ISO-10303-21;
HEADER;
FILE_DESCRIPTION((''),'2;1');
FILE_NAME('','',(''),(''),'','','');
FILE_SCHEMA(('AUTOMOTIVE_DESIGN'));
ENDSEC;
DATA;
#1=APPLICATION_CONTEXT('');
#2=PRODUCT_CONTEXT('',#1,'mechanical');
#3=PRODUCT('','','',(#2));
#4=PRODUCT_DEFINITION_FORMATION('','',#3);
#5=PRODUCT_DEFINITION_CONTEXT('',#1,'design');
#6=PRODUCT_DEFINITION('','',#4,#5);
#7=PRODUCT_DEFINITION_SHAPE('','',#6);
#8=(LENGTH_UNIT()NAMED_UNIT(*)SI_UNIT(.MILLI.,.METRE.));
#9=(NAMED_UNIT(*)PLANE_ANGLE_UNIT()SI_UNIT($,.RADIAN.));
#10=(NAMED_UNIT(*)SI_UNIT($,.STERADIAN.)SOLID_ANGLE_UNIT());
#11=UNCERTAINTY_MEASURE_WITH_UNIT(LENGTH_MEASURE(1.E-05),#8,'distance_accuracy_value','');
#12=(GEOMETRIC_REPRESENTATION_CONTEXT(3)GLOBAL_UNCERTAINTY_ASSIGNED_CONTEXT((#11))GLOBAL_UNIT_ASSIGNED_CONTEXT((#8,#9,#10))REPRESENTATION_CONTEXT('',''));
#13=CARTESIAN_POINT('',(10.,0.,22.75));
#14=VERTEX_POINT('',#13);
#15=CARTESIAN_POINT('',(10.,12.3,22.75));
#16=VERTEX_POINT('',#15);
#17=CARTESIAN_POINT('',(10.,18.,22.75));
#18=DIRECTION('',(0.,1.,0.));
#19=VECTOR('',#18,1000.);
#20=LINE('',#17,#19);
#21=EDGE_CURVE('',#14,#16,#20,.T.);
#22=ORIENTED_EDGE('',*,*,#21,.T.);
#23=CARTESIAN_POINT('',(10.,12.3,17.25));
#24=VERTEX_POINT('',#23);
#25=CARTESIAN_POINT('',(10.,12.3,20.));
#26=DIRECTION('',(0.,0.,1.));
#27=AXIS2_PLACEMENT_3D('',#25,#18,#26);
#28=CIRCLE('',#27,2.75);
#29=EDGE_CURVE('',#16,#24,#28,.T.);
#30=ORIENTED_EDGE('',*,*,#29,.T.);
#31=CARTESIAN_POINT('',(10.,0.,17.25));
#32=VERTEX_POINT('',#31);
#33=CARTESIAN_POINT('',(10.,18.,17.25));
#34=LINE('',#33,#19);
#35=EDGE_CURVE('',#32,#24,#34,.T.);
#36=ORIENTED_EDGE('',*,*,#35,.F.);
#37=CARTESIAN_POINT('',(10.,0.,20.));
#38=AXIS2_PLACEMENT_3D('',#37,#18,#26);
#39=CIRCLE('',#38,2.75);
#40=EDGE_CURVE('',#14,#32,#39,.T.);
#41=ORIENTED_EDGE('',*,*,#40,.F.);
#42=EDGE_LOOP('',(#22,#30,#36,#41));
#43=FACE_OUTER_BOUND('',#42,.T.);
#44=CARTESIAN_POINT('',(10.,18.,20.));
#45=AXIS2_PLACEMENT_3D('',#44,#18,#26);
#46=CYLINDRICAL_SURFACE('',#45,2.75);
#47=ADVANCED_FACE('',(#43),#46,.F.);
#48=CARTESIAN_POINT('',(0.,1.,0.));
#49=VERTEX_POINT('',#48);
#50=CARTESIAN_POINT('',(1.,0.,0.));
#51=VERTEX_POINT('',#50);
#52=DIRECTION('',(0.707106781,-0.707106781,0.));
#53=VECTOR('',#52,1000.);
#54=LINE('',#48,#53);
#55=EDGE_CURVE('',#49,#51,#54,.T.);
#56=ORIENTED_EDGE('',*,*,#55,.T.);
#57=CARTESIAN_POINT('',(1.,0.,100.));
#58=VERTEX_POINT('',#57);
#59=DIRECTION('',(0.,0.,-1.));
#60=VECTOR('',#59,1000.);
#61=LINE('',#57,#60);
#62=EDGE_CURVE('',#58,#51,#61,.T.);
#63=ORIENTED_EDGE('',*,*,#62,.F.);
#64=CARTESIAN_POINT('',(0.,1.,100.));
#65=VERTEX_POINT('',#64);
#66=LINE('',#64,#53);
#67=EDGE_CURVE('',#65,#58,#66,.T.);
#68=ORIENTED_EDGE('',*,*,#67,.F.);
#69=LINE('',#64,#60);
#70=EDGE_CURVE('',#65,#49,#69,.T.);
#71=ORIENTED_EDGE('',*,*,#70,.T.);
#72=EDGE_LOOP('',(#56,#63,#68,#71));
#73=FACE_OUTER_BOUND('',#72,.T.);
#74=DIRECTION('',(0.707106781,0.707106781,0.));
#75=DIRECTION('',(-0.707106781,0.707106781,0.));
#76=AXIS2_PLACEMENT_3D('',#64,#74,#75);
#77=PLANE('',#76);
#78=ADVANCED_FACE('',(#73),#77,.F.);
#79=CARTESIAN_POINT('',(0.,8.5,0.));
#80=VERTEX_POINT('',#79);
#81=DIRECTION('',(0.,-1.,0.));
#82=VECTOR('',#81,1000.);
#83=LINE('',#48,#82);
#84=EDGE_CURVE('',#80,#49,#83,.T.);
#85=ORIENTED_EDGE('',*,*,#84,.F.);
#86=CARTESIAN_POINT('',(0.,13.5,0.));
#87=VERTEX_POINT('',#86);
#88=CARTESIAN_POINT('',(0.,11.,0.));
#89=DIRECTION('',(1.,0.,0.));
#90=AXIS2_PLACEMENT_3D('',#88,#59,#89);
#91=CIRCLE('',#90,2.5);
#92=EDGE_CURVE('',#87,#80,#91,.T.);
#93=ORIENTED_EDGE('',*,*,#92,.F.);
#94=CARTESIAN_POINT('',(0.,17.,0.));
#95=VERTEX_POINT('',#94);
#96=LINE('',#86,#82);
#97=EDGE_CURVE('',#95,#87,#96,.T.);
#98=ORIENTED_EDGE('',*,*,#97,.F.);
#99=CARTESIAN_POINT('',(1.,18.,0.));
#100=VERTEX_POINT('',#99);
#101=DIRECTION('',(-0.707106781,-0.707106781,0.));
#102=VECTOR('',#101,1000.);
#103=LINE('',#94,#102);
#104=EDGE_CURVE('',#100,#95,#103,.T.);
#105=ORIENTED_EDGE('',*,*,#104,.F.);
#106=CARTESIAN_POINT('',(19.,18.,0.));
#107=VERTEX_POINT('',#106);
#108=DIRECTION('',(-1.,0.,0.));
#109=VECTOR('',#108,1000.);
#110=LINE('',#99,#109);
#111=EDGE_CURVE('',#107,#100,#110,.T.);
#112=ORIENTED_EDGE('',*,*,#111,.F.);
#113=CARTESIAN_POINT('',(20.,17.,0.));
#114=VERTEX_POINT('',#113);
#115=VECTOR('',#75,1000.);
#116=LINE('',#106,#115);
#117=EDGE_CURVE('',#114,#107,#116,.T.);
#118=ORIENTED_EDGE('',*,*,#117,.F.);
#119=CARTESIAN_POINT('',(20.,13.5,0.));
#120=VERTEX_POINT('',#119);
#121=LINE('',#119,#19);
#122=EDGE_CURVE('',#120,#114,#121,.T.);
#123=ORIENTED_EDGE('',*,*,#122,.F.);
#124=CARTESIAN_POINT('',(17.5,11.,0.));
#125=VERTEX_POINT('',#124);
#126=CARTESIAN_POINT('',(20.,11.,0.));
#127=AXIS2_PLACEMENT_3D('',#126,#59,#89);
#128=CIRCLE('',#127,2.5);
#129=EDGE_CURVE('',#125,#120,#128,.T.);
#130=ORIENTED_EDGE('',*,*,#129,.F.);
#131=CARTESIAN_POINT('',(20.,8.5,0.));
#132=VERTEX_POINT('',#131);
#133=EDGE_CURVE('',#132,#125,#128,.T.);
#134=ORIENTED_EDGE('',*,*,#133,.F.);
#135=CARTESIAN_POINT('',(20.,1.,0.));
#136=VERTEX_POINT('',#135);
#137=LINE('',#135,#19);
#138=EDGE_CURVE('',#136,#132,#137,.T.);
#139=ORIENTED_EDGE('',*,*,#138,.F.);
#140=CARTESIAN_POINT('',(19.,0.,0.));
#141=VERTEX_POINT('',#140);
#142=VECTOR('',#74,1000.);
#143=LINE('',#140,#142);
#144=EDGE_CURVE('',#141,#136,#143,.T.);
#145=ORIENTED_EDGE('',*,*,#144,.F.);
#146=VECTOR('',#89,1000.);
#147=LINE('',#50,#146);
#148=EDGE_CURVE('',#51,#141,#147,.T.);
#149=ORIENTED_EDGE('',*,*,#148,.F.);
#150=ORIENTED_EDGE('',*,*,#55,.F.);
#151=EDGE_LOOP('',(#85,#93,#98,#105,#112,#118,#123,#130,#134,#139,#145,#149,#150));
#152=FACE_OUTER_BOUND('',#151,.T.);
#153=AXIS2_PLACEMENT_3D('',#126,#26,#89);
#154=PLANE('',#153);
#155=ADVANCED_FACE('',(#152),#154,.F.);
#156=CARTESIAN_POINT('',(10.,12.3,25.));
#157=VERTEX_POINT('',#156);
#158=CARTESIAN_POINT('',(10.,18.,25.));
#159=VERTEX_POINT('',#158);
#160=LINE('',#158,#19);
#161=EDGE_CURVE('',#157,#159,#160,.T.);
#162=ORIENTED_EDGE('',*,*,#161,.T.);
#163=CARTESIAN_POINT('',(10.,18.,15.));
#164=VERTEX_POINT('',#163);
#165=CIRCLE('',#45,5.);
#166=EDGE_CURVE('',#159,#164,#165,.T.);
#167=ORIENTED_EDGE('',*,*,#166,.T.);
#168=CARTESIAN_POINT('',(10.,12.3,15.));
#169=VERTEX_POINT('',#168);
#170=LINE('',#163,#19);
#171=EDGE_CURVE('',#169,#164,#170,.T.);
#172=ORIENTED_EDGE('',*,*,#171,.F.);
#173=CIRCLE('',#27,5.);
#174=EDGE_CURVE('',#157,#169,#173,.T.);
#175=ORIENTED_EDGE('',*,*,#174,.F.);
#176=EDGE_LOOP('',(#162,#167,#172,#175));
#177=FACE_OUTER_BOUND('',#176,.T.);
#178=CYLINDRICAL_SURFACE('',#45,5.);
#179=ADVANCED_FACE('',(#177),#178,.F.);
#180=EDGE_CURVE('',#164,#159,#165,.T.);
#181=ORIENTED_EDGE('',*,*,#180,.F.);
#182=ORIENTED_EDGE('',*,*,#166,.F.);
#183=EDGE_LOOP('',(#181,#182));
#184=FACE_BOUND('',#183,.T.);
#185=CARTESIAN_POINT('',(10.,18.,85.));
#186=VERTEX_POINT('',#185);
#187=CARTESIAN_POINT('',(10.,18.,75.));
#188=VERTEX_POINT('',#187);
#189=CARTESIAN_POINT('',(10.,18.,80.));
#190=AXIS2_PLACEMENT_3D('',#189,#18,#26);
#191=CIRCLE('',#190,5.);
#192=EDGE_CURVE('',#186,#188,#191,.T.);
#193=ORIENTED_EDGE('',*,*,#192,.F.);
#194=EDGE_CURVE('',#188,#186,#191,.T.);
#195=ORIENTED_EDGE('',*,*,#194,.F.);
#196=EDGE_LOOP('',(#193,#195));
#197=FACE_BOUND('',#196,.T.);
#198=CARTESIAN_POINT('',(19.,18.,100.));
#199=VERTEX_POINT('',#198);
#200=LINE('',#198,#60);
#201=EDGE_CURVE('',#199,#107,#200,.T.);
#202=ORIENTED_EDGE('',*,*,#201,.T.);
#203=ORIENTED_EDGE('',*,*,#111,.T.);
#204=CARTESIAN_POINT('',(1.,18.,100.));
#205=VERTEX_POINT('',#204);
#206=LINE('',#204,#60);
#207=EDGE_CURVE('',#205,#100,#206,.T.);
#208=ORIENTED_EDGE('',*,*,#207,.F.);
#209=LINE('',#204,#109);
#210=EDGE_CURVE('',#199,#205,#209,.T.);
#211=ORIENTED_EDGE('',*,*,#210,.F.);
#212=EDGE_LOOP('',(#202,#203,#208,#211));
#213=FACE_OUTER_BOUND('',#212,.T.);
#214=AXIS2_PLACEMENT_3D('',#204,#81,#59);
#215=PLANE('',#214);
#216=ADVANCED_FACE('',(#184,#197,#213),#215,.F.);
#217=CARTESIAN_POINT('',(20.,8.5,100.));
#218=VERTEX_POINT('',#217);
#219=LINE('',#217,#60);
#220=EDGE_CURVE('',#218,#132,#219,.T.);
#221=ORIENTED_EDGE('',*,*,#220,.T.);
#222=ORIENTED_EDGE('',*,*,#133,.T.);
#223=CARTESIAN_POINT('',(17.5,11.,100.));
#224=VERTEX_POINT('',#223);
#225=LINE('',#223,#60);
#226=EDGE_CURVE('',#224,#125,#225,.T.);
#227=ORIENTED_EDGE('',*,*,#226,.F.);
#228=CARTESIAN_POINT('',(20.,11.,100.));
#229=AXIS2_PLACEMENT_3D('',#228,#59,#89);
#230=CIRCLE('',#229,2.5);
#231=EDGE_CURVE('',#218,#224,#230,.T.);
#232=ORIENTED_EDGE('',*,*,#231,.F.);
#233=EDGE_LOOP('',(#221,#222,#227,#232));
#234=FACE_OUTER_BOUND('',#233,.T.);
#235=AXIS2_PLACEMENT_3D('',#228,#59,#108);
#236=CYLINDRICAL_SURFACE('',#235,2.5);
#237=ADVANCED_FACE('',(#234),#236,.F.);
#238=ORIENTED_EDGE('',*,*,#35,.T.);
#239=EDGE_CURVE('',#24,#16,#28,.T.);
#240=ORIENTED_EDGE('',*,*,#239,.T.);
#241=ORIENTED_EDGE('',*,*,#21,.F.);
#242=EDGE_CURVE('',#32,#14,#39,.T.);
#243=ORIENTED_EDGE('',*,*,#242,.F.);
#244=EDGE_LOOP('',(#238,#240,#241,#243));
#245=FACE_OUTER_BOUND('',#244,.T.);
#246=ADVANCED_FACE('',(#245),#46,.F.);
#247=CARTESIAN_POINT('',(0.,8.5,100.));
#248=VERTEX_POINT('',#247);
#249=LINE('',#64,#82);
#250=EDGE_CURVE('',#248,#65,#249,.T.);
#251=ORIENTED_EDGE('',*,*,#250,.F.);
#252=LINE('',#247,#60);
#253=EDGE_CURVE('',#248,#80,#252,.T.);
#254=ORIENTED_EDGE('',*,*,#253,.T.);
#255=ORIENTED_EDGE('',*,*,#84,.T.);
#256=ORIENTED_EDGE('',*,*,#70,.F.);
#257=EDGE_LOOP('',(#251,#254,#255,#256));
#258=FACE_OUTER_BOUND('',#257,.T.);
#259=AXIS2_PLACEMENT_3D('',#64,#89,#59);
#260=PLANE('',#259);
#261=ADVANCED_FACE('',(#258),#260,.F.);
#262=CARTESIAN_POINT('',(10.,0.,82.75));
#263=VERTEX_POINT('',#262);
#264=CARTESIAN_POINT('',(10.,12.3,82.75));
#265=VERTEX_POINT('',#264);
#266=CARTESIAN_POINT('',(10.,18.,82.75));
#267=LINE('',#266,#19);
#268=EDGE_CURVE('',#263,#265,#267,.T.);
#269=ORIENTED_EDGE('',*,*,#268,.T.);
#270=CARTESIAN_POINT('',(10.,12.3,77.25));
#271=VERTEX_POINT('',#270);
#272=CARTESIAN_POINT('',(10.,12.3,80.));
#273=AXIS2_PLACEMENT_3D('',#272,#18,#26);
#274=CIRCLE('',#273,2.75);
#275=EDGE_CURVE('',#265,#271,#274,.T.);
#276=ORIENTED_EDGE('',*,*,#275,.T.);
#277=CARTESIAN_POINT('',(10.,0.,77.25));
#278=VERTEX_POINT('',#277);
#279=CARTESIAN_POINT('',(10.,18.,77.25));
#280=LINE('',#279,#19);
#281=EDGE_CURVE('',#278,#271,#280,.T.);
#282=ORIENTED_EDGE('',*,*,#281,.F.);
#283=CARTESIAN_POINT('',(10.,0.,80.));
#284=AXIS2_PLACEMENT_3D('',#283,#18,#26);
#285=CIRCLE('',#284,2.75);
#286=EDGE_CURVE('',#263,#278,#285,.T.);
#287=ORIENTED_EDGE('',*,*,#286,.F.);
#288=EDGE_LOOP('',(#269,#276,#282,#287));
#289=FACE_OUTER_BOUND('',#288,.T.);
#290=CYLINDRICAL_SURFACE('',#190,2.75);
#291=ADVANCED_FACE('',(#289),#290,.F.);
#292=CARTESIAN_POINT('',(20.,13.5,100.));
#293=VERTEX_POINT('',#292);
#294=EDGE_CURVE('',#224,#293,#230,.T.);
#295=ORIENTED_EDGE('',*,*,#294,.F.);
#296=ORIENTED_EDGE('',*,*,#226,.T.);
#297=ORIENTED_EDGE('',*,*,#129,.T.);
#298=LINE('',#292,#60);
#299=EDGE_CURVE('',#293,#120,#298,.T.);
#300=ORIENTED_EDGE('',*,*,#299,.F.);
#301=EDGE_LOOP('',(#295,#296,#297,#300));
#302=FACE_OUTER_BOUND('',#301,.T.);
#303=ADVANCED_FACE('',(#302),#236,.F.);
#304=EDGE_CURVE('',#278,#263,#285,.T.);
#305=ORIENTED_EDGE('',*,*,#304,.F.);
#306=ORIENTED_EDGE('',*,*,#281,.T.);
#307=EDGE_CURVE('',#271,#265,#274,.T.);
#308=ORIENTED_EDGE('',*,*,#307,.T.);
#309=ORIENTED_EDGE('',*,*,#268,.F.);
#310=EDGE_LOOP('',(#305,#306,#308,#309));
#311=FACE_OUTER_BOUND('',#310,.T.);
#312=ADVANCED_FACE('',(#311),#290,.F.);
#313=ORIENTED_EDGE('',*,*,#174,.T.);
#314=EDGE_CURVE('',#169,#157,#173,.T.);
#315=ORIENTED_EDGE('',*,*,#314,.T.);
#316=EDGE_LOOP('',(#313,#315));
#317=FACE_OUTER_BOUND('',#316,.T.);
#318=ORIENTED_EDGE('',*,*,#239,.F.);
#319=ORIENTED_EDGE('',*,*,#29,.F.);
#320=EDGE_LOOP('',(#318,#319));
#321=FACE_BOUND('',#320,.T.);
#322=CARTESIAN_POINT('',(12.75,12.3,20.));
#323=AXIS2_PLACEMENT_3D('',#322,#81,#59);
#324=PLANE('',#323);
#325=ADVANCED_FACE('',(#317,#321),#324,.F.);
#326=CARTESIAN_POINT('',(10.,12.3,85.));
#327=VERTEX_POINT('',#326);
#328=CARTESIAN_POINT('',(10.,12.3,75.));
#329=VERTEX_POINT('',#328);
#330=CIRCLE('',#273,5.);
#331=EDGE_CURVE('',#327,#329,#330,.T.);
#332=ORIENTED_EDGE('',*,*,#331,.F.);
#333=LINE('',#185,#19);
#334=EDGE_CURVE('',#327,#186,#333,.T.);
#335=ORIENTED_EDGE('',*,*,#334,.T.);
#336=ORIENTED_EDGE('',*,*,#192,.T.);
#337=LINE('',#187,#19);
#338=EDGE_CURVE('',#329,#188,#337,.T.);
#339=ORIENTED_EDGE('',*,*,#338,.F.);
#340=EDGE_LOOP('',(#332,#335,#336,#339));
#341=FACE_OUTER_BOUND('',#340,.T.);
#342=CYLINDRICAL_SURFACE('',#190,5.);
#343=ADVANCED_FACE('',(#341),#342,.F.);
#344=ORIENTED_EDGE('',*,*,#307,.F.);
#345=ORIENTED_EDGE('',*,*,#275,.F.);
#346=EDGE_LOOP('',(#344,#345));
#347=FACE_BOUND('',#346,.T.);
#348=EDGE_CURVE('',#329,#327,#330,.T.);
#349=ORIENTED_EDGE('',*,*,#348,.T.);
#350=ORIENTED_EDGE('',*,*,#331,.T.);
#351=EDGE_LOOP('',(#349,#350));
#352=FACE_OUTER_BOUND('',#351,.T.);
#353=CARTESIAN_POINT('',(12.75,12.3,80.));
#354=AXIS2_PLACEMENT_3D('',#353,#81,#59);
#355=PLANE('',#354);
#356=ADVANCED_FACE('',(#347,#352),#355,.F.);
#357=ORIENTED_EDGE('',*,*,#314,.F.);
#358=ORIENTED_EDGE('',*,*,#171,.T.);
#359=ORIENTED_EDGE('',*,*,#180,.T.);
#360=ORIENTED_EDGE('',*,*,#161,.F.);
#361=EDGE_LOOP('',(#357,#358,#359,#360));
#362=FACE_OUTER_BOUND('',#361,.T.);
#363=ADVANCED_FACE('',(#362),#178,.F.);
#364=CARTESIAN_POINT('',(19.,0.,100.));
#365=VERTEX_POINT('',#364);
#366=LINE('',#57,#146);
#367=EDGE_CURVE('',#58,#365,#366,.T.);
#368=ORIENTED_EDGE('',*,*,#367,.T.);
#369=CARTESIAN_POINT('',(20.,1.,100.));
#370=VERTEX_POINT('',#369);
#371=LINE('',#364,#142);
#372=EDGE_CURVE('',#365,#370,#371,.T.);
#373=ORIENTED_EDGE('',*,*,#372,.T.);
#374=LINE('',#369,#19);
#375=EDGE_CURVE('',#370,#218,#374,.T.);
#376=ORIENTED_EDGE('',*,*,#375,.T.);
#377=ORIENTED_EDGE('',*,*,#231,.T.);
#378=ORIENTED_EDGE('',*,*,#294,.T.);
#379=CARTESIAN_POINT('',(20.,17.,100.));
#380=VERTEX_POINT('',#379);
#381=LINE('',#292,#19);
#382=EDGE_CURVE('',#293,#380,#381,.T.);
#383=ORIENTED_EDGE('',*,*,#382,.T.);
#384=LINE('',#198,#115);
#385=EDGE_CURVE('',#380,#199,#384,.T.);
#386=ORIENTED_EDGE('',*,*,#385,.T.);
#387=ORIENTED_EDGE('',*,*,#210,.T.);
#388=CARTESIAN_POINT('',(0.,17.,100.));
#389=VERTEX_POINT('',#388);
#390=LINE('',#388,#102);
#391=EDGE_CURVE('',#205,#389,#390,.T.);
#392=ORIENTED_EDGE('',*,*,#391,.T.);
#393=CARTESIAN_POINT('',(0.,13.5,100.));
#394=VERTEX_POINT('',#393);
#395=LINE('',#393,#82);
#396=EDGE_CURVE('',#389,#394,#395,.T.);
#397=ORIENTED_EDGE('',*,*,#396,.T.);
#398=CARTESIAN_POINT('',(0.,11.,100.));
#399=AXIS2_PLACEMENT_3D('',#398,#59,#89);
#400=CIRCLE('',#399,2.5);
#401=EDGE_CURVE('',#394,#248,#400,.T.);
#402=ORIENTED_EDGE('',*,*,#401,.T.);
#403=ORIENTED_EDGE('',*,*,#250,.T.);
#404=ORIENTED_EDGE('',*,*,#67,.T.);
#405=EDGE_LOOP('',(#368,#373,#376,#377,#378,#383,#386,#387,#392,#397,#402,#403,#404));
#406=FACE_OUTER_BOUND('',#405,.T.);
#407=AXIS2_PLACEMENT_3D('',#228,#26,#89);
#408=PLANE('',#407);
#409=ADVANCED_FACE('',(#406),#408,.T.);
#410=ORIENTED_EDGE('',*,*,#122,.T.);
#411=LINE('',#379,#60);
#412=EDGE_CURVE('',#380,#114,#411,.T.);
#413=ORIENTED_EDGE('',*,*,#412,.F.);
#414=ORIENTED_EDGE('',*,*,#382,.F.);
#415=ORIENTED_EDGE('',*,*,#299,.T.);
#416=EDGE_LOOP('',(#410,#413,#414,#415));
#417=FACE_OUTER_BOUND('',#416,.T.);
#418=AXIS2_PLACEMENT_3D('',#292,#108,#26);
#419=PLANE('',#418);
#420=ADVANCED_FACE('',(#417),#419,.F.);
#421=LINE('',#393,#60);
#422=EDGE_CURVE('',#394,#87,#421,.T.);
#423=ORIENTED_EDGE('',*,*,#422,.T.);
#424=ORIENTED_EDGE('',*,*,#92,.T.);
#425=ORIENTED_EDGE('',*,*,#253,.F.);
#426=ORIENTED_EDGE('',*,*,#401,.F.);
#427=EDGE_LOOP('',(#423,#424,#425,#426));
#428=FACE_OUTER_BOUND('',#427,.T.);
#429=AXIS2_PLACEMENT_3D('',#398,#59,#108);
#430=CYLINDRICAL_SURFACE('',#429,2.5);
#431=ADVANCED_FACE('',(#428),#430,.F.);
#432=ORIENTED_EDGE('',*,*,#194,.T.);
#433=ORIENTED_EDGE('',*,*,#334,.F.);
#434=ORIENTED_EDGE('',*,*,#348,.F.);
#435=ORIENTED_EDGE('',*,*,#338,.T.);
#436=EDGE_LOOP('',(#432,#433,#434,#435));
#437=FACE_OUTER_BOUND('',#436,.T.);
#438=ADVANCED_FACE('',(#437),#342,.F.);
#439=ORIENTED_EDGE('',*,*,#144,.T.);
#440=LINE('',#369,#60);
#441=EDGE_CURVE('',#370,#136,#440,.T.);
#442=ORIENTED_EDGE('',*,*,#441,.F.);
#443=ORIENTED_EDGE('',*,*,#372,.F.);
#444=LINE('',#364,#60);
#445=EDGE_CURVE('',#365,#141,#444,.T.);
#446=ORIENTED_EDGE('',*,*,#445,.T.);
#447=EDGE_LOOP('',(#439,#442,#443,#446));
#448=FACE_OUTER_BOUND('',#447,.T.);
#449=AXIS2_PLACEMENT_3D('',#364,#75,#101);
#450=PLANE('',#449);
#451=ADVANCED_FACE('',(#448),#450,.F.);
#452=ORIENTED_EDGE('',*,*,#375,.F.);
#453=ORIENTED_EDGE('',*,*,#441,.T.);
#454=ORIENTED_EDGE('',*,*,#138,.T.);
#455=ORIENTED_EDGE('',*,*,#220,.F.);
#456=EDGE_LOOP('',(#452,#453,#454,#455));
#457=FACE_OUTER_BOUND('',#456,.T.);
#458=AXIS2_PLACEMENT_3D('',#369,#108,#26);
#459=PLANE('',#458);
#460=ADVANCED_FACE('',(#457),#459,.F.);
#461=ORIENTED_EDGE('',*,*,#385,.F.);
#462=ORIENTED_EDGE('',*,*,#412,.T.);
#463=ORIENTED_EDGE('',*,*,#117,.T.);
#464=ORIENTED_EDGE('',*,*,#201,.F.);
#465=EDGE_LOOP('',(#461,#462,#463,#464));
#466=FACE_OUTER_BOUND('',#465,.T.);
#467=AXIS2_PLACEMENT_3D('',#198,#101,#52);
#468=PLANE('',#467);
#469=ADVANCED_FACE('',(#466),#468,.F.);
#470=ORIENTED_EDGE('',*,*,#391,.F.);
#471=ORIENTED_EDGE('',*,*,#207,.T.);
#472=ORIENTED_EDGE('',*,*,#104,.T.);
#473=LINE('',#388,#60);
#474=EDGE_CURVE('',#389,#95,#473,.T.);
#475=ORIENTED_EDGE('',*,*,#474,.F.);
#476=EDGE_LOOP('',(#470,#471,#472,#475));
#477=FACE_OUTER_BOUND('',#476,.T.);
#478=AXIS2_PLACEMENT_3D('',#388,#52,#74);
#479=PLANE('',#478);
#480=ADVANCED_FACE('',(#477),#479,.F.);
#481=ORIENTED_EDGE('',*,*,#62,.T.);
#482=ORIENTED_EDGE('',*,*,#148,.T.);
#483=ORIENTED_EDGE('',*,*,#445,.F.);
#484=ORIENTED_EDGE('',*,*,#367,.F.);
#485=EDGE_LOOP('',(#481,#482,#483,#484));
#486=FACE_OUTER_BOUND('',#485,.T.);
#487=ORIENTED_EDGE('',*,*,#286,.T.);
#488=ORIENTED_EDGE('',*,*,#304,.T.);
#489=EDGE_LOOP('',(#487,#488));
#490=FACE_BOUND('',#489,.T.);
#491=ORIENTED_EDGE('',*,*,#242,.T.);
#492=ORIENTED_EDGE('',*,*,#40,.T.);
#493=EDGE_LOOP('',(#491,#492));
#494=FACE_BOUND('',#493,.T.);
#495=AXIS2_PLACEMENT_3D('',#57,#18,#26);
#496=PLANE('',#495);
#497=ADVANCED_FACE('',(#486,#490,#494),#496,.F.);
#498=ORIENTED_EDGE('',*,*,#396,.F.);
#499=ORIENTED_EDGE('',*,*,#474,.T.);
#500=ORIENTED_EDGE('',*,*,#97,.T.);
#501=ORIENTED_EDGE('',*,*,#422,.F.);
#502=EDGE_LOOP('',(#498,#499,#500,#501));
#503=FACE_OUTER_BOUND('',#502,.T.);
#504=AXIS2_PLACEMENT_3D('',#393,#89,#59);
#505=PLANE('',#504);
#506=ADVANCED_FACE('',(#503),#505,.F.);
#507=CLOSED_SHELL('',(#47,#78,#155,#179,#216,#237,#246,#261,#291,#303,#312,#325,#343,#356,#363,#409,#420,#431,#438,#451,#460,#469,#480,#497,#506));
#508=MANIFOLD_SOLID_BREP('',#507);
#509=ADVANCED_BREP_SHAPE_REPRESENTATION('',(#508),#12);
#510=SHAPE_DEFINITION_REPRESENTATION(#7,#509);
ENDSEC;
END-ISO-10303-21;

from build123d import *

# Parameters (mm, degrees)
EXTRUDE1_DEPTH                                       = 100
HOLE_SIZE_PER_SOCKET_HEAD_CAP_SCREW_TYPE_D           = 5.5
HOLE_SIZE_PER_SOCKET_HEAD_CAP_SCREW_TYPE_CBORE_D     = 10
HOLE_SIZE_PER_SOCKET_HEAD_CAP_SCREW_TYPE_CBORE_DEPTH = 5.7


with BuildPart() as part:
    # Sketch1 → Extrude1 (new body)
    with BuildSketch(Plane.XY):
        with BuildLine():
            Line((0, 13.5), (0, 17))
            Line((0, 17), (1, 18))
            Line((1, 18), (19, 18))
            Line((19, 18), (20, 17))
            Line((20, 17), (20, 13.5))
            ThreePointArc((20, 13.5), (17.5, 11), (20, 8.5))
            Line((20, 8.5), (20, 1))
            Line((20, 1), (19, 0))
            Line((19, 0), (1, 0))
            Line((1, 0), (0, 1))
            Line((0, 1), (0, 8.5))
            ThreePointArc((0, 8.5), (2.5, 11), (0, 13.5))
        make_face()
    extrude(amount=EXTRUDE1_DEPTH)

    # Hole size per socket head cap screw type 1 (through all)
    with Locations(Plane(origin=(10, 18, 20), x_dir=(0, 0, 1), z_dir=(0, 1, 0))):
        with Locations((0, 0), (60, 0)):
            CounterBoreHole(HOLE_SIZE_PER_SOCKET_HEAD_CAP_SCREW_TYPE_D / 2, HOLE_SIZE_PER_SOCKET_HEAD_CAP_SCREW_TYPE_CBORE_D / 2, HOLE_SIZE_PER_SOCKET_HEAD_CAP_SCREW_TYPE_CBORE_DEPTH)


solid = part.part
